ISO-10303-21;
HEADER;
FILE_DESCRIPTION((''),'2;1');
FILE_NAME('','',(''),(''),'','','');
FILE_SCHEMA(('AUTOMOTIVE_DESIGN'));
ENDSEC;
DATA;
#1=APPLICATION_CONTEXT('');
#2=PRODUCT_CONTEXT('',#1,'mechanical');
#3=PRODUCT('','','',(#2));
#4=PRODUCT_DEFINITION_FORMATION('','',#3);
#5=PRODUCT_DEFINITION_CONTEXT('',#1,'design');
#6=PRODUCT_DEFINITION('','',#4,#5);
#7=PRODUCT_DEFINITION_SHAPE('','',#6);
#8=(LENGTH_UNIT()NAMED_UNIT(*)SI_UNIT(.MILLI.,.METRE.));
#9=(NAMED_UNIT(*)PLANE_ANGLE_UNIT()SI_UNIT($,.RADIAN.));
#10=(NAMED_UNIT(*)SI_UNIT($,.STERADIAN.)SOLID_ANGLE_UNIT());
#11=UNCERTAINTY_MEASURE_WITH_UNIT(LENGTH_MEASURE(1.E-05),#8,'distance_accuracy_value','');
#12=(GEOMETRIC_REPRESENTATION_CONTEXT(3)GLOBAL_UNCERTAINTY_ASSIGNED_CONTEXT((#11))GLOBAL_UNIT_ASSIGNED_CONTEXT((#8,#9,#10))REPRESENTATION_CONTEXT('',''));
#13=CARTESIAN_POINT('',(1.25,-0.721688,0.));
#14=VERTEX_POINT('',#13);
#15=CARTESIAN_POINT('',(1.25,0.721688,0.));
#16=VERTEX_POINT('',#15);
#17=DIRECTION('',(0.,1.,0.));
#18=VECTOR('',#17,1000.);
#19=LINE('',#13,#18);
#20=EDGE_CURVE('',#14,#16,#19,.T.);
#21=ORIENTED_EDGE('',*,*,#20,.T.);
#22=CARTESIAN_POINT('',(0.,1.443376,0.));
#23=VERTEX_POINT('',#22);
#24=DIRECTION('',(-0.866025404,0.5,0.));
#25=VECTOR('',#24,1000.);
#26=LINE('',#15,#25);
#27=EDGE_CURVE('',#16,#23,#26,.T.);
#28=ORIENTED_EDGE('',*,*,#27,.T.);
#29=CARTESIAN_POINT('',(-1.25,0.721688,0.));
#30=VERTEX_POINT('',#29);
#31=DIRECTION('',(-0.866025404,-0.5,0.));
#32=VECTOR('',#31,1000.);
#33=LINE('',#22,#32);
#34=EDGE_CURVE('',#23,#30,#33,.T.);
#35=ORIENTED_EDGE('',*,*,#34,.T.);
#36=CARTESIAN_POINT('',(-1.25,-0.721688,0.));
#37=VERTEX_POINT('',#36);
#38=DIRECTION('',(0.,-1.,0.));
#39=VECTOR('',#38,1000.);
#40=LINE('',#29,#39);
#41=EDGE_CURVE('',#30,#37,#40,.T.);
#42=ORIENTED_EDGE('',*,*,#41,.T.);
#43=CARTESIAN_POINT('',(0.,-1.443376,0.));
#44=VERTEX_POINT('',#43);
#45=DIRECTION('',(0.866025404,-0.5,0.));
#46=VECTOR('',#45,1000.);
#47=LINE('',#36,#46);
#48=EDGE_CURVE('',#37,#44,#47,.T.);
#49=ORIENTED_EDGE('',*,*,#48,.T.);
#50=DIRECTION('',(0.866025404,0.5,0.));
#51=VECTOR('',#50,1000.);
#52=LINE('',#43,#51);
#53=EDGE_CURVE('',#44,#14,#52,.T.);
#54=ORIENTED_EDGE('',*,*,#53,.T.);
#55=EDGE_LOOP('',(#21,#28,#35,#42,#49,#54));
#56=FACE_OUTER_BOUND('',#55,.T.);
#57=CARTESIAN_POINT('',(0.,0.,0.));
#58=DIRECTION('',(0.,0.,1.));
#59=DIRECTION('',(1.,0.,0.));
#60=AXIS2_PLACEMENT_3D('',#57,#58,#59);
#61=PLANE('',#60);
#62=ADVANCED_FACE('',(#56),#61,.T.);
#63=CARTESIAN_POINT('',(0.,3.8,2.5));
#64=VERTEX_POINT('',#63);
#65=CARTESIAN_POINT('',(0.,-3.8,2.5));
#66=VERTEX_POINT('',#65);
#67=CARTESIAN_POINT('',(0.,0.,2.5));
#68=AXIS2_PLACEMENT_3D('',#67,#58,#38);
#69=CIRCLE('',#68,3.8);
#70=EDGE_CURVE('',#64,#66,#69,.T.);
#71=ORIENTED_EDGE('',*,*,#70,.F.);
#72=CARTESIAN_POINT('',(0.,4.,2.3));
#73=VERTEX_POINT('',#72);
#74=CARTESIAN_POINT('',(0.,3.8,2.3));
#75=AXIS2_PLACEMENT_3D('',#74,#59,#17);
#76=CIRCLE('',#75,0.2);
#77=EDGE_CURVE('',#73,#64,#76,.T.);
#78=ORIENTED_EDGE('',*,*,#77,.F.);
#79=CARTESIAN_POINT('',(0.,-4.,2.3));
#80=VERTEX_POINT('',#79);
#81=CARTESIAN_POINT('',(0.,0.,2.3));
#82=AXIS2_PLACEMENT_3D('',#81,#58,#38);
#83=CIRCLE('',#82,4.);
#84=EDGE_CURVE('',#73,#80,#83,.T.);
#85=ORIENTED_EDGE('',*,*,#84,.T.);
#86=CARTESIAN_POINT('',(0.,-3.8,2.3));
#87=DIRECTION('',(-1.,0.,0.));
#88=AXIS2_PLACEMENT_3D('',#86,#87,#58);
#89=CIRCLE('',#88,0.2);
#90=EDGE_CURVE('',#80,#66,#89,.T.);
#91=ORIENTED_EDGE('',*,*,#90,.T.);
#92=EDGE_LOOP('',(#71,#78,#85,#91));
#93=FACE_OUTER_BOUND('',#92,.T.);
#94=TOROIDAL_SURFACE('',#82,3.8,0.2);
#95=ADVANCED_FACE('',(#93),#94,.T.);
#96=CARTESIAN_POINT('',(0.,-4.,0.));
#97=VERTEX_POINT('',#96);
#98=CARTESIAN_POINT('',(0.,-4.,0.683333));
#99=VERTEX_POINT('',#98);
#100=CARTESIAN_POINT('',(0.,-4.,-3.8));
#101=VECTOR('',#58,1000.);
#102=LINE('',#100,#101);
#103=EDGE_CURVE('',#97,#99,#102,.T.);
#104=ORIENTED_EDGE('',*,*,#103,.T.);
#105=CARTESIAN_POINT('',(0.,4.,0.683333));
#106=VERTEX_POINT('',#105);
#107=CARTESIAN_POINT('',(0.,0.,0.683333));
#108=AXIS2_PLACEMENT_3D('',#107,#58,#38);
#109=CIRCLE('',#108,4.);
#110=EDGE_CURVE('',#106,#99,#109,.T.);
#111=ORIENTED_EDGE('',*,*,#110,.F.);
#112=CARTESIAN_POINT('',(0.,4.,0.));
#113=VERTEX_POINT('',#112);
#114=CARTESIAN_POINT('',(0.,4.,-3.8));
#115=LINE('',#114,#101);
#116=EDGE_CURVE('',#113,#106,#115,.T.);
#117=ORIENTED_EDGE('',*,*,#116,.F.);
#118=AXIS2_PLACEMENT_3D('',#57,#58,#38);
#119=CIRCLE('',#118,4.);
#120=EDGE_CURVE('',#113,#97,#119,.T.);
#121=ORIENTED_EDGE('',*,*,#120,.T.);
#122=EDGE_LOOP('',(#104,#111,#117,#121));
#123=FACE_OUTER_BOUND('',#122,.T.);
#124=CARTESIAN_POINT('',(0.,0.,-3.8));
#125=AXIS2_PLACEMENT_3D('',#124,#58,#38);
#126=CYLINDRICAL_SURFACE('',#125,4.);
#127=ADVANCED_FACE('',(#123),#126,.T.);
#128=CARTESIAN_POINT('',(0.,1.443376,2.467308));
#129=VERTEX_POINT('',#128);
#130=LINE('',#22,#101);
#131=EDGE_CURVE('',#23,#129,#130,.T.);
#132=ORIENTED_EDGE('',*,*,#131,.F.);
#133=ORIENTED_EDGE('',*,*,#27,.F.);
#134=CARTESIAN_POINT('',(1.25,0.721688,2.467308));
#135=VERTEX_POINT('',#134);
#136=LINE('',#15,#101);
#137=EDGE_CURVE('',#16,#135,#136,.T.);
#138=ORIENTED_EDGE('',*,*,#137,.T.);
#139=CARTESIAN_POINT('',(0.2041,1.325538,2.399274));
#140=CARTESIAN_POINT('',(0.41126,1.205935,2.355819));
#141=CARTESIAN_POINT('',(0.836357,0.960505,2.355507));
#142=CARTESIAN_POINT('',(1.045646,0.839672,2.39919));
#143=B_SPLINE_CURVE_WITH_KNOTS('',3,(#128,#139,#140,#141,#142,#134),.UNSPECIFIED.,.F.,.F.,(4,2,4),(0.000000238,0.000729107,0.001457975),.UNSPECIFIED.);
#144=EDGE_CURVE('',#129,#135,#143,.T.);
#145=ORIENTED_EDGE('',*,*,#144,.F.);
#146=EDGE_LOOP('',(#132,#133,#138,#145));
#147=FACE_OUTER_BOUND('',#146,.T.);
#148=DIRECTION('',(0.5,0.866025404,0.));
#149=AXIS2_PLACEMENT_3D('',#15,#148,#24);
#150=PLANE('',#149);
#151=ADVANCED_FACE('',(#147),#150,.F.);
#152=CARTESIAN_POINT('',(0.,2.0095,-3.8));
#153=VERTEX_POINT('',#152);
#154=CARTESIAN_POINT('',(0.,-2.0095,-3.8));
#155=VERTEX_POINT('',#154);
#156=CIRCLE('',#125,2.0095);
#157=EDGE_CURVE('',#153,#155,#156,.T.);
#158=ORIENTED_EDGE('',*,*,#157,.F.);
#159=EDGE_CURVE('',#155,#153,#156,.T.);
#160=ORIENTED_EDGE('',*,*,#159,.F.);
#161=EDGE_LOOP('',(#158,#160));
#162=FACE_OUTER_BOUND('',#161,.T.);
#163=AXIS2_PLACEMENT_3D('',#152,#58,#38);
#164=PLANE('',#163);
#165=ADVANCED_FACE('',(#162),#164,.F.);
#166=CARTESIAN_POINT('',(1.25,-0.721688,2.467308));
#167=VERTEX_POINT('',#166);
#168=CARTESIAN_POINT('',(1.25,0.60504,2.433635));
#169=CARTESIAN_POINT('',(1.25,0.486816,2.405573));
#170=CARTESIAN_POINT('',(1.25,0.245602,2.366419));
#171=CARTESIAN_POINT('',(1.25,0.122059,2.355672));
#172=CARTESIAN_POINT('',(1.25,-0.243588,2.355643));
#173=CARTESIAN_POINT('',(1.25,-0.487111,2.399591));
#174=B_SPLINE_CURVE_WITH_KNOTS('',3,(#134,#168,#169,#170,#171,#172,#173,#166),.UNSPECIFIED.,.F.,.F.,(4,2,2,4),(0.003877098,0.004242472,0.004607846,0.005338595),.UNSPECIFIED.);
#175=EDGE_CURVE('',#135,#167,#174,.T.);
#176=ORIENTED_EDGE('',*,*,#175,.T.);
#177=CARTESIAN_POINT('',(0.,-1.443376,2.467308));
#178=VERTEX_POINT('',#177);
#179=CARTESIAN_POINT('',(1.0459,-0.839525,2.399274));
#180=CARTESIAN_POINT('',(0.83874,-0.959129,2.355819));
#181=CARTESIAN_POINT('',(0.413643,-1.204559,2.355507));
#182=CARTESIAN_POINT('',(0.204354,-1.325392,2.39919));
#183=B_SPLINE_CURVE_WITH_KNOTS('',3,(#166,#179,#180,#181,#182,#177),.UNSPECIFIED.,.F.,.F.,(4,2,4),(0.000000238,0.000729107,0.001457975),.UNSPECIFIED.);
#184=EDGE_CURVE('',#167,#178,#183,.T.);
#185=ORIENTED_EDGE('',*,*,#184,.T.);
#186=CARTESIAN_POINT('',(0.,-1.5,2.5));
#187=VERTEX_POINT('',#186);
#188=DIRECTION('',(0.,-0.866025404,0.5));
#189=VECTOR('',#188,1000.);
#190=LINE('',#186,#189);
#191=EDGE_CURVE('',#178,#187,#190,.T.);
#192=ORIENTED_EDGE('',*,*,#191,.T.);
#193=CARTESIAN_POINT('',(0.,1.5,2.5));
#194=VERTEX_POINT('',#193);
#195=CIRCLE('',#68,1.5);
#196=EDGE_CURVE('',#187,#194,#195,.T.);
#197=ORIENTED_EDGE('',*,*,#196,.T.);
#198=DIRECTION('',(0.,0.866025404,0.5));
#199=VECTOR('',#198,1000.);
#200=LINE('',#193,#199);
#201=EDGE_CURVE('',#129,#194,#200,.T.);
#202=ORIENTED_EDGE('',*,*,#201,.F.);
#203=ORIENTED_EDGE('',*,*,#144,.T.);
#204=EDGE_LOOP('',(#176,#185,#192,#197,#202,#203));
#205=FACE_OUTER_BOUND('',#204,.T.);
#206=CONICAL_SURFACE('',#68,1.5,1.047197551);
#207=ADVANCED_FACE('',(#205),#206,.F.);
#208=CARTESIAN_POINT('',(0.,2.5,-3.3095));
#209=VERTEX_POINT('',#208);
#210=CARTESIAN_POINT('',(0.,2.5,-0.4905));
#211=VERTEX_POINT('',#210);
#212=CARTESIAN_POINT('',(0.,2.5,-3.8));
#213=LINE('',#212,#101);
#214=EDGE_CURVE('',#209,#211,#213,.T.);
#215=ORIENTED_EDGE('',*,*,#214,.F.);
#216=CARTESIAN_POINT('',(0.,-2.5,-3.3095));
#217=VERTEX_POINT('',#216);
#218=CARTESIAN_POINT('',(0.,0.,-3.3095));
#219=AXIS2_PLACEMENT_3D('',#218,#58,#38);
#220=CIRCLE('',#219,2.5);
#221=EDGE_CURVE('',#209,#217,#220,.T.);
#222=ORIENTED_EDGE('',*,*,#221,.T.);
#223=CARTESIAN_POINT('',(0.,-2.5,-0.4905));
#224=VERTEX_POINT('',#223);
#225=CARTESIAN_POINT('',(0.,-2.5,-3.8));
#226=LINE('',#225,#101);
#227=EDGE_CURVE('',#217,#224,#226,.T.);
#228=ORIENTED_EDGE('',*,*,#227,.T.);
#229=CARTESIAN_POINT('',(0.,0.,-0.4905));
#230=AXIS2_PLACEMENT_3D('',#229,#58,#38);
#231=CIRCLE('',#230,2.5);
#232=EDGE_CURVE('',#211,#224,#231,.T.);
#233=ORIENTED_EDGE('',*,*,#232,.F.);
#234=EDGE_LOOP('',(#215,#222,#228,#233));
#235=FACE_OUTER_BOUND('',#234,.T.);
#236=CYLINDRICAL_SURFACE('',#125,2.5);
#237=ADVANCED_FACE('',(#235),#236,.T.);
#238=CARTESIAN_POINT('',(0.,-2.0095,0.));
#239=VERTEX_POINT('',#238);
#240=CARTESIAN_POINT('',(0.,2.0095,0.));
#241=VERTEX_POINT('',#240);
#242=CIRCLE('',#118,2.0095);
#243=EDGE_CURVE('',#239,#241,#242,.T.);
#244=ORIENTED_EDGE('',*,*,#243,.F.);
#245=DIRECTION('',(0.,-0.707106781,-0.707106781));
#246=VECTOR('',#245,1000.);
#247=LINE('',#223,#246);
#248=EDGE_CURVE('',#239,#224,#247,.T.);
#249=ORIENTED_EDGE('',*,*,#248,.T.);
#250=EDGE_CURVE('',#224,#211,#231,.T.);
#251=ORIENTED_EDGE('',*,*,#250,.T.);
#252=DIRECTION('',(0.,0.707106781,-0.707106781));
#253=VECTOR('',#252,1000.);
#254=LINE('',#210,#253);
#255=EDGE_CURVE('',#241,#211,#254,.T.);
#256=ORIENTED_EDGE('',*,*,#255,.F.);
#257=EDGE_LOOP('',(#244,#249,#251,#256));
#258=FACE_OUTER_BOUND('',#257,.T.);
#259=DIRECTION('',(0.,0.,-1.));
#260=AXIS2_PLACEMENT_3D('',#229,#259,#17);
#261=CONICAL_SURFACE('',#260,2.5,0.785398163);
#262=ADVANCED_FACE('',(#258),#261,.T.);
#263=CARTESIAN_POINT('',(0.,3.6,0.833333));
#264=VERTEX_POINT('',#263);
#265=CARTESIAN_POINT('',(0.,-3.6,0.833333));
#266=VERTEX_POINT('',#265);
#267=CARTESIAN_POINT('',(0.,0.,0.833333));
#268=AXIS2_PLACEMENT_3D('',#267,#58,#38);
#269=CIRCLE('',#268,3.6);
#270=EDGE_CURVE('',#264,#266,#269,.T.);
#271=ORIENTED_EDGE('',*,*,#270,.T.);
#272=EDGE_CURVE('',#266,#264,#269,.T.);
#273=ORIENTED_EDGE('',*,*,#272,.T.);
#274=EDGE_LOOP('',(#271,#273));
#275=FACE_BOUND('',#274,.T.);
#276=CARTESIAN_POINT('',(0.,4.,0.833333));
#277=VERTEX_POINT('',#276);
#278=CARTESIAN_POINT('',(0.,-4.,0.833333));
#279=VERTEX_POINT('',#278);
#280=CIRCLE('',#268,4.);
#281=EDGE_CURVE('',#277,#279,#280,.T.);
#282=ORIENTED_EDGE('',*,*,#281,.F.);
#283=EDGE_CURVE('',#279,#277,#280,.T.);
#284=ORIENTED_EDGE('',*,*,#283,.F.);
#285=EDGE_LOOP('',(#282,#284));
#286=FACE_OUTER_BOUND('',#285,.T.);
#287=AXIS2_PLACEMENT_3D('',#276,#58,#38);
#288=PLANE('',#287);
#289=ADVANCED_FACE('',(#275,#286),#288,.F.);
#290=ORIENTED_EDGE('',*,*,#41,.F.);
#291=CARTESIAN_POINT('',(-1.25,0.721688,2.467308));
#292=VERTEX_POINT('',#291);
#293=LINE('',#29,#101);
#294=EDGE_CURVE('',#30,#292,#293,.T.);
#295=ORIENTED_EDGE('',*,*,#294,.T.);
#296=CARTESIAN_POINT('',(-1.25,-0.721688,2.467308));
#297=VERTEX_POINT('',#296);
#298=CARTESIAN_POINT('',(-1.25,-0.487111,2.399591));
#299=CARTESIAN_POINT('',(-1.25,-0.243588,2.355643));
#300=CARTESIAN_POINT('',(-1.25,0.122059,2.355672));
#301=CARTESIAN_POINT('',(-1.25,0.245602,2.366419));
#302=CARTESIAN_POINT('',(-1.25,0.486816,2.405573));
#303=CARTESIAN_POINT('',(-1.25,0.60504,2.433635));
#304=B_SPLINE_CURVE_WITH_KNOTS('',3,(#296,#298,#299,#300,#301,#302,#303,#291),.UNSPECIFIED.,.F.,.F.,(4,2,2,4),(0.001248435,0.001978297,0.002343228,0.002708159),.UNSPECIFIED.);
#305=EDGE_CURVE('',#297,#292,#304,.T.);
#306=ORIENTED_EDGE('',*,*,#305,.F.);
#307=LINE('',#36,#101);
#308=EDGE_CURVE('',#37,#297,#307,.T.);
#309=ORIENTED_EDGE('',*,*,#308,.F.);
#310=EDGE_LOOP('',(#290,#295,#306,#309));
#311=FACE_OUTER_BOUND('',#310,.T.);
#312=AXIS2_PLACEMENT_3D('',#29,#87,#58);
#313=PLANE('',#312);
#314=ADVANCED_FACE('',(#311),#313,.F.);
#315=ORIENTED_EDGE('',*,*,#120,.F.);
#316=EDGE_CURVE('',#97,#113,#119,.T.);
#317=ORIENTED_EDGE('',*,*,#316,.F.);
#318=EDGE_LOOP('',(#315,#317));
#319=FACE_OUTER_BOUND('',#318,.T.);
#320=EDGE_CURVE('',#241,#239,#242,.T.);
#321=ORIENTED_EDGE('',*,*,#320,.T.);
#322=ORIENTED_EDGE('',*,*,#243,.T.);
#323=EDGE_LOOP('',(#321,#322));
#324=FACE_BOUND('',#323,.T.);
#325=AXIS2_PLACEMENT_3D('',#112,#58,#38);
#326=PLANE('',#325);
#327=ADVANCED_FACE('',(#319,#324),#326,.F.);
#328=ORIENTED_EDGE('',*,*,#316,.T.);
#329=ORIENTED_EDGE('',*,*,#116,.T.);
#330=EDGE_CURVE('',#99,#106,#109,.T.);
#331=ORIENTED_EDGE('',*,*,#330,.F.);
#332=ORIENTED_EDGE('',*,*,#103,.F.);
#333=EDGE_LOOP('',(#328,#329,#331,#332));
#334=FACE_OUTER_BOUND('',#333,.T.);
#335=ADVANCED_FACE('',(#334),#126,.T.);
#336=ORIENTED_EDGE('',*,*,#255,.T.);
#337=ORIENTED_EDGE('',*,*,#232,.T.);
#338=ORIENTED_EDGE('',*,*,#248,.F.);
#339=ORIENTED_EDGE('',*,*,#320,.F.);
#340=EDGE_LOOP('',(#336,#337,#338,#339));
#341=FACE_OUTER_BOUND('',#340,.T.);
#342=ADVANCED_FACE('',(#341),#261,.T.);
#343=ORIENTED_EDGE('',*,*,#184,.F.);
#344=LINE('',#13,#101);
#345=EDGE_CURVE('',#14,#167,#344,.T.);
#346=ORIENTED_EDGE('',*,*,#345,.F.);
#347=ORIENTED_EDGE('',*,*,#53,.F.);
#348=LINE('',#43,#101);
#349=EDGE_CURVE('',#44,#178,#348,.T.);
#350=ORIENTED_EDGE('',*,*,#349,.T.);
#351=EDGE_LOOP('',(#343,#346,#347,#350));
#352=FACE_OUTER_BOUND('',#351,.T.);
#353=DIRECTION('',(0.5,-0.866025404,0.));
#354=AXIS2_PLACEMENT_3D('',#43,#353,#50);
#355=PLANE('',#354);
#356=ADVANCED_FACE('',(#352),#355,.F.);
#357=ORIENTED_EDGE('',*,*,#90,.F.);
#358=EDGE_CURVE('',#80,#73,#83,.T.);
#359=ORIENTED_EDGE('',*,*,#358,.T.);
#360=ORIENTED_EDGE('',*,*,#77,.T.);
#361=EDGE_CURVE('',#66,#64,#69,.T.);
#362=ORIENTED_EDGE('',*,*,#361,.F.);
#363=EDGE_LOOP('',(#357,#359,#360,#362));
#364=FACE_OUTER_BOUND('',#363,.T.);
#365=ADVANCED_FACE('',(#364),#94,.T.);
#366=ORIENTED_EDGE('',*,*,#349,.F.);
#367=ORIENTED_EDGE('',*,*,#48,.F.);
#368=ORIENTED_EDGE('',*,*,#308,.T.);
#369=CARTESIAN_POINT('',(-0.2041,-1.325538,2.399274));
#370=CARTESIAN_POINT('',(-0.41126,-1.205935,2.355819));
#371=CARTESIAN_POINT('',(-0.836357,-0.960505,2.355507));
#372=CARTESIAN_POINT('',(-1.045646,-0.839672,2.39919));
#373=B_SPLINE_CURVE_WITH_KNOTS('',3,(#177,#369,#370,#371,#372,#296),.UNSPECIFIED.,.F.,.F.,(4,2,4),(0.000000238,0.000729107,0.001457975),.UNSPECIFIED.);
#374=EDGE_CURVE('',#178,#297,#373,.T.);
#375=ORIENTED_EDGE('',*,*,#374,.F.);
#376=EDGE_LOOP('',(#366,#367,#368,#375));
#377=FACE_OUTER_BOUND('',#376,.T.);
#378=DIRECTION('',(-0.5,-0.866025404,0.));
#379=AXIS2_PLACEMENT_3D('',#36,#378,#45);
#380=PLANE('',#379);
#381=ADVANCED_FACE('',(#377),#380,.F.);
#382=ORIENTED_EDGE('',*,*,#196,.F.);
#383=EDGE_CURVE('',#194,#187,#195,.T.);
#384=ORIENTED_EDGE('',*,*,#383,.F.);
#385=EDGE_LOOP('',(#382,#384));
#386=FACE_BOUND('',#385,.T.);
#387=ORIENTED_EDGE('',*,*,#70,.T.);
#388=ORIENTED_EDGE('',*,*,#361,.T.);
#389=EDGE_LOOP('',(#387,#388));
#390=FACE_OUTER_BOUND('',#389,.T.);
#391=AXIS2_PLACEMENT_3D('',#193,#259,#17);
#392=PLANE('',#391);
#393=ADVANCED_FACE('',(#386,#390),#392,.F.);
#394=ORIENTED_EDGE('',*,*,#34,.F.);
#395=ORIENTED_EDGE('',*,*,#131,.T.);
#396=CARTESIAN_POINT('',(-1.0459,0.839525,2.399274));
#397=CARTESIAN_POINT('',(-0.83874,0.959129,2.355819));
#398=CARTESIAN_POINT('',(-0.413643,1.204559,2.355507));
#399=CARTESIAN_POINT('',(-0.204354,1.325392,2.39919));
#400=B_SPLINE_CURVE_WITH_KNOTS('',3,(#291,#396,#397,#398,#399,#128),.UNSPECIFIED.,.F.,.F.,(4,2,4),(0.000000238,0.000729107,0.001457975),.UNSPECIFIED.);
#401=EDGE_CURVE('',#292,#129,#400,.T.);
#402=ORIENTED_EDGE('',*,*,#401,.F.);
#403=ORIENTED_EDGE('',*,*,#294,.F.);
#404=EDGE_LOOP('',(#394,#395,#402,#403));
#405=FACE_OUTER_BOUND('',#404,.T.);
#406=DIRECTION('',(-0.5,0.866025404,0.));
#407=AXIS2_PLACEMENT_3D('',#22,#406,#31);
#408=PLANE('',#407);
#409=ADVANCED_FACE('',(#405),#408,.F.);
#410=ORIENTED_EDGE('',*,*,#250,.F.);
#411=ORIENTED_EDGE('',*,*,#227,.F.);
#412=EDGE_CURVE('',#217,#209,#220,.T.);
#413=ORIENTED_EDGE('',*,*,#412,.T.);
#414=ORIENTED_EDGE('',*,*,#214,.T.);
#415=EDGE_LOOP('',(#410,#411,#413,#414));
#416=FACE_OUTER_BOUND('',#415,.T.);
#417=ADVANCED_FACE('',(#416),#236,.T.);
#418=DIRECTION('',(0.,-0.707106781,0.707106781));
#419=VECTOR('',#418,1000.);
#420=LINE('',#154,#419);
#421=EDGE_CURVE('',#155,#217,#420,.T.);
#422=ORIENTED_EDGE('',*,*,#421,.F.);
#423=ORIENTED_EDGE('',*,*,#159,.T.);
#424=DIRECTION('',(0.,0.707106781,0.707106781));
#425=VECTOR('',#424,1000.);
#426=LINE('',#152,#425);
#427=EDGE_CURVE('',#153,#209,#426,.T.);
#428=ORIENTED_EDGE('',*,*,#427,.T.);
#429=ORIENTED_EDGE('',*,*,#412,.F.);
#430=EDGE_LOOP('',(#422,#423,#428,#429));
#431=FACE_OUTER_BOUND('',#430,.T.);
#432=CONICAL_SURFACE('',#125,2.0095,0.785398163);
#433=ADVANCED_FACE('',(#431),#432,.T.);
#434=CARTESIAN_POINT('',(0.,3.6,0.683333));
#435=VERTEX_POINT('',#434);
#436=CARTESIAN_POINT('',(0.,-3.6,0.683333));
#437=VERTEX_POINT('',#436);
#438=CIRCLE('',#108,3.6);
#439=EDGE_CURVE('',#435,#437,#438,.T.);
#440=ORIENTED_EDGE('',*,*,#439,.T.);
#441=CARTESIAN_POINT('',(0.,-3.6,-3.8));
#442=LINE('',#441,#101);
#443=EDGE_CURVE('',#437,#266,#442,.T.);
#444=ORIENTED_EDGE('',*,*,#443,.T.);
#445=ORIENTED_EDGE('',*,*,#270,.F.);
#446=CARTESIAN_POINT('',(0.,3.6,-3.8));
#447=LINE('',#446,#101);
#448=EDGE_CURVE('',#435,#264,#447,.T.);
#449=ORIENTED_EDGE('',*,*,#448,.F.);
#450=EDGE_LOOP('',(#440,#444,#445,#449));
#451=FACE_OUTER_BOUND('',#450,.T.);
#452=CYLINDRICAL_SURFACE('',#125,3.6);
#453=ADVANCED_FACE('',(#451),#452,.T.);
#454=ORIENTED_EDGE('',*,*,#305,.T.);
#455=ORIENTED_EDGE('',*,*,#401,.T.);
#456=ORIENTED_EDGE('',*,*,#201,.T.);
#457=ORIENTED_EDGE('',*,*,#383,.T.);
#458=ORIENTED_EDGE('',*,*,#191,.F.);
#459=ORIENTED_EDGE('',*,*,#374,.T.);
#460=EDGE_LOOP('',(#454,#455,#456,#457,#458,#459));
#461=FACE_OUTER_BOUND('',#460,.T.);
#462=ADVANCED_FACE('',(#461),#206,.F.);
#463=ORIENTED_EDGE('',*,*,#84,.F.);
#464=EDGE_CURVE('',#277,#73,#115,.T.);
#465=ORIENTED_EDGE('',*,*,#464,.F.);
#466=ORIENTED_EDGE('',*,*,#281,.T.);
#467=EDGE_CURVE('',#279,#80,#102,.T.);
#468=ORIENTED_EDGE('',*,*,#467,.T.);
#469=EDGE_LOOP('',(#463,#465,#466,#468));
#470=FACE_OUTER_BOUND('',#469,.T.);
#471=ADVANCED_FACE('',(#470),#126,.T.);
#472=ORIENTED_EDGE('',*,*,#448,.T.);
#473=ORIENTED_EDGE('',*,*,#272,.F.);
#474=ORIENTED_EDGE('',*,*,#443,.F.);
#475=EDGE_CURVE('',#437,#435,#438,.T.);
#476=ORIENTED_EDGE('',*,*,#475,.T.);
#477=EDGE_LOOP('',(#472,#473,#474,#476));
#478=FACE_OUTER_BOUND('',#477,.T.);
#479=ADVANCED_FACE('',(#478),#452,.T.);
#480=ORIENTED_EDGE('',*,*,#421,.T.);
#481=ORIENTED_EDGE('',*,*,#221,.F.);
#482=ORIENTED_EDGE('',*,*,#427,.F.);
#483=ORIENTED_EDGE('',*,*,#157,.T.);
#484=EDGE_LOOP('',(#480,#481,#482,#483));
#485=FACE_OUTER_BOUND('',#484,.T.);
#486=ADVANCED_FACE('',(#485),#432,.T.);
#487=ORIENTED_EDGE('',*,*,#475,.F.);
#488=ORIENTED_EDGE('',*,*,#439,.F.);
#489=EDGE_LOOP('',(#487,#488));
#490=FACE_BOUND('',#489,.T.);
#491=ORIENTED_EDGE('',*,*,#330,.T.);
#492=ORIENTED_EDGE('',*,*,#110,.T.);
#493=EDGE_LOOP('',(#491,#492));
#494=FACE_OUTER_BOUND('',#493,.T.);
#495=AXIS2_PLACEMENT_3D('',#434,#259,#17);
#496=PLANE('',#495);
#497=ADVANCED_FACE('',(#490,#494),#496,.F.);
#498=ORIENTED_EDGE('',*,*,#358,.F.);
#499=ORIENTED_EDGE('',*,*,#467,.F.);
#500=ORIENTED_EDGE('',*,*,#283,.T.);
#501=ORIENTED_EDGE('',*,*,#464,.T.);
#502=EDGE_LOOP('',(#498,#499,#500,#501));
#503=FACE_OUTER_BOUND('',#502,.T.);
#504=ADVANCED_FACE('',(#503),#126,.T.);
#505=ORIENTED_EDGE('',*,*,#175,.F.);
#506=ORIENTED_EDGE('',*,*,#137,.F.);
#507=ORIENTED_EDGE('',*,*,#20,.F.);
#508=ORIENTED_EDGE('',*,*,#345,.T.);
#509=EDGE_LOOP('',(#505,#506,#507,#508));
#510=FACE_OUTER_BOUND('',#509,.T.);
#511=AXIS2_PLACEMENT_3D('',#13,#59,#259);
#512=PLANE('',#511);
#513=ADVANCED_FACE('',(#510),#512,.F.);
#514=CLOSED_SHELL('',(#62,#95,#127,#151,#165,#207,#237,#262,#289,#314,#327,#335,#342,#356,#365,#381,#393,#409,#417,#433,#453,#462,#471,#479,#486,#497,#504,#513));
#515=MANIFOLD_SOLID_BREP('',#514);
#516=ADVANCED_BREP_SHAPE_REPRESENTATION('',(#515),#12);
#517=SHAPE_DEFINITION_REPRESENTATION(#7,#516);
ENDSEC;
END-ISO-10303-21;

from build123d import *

# Parameters (mm, degrees)
CUT_EXTRUDE1_DEPTH = 2.5


with BuildPart() as part:
    # Sketch1 → Revolve1 (revolve)
    with BuildSketch(Plane(origin=(0, 0, 0), x_dir=(0, 0, -1), z_dir=(1, 0, 0)), mode=Mode.PRIVATE) as revolve1_sk:
        with BuildLine():
            Line((-1.633974596, 0), (-2.5, 1.5))
            Line((-2.5, 1.5), (-2.5, 3.8))
            ThreePointArc((-2.5, 3.8), (-2.441421356, 3.941421356), (-2.3, 4))
            Line((-2.3, 4), (-0.833333333, 4))
            Line((-0.833333333, 4), (-0.833333333, 3.6))
            Line((-0.833333333, 3.6), (-0.683333333, 3.6))
            Line((-0.683333333, 3.6), (-0.683333333, 4))
            Line((-0.683333333, 4), (0, 4))
            Line((0, 4), (0, 2.0095))
            Line((0, 2.0095), (0.4905, 2.5))
            Line((0.4905, 2.5), (3.3095, 2.5))
            Line((3.3095, 2.5), (3.8, 2.0095))
            Line((3.8, 2.0095), (3.8, 0))
            Line((3.8, 0), (-1.633974596, 0))
        make_face()
    revolve(revolve1_sk.sketch.rotate(Axis((0, 0, -3.8), (0, 0, 1)), 180), axis=Axis((0, 0, -3.8), (0, 0, 1)))

    # Sketch2 → Cut-Extrude1 (cut)
    with BuildSketch(Plane.XY.offset(2.5)):
        Polygon((-1.25, -0.721687836), (0, -1.443375673), (1.25, -0.721687836), (1.25, 0.721687836), (0, 1.443375673), (-1.25, 0.721687836), align=None)
    extrude(amount=-CUT_EXTRUDE1_DEPTH, mode=Mode.SUBTRACT)


solid = part.part
